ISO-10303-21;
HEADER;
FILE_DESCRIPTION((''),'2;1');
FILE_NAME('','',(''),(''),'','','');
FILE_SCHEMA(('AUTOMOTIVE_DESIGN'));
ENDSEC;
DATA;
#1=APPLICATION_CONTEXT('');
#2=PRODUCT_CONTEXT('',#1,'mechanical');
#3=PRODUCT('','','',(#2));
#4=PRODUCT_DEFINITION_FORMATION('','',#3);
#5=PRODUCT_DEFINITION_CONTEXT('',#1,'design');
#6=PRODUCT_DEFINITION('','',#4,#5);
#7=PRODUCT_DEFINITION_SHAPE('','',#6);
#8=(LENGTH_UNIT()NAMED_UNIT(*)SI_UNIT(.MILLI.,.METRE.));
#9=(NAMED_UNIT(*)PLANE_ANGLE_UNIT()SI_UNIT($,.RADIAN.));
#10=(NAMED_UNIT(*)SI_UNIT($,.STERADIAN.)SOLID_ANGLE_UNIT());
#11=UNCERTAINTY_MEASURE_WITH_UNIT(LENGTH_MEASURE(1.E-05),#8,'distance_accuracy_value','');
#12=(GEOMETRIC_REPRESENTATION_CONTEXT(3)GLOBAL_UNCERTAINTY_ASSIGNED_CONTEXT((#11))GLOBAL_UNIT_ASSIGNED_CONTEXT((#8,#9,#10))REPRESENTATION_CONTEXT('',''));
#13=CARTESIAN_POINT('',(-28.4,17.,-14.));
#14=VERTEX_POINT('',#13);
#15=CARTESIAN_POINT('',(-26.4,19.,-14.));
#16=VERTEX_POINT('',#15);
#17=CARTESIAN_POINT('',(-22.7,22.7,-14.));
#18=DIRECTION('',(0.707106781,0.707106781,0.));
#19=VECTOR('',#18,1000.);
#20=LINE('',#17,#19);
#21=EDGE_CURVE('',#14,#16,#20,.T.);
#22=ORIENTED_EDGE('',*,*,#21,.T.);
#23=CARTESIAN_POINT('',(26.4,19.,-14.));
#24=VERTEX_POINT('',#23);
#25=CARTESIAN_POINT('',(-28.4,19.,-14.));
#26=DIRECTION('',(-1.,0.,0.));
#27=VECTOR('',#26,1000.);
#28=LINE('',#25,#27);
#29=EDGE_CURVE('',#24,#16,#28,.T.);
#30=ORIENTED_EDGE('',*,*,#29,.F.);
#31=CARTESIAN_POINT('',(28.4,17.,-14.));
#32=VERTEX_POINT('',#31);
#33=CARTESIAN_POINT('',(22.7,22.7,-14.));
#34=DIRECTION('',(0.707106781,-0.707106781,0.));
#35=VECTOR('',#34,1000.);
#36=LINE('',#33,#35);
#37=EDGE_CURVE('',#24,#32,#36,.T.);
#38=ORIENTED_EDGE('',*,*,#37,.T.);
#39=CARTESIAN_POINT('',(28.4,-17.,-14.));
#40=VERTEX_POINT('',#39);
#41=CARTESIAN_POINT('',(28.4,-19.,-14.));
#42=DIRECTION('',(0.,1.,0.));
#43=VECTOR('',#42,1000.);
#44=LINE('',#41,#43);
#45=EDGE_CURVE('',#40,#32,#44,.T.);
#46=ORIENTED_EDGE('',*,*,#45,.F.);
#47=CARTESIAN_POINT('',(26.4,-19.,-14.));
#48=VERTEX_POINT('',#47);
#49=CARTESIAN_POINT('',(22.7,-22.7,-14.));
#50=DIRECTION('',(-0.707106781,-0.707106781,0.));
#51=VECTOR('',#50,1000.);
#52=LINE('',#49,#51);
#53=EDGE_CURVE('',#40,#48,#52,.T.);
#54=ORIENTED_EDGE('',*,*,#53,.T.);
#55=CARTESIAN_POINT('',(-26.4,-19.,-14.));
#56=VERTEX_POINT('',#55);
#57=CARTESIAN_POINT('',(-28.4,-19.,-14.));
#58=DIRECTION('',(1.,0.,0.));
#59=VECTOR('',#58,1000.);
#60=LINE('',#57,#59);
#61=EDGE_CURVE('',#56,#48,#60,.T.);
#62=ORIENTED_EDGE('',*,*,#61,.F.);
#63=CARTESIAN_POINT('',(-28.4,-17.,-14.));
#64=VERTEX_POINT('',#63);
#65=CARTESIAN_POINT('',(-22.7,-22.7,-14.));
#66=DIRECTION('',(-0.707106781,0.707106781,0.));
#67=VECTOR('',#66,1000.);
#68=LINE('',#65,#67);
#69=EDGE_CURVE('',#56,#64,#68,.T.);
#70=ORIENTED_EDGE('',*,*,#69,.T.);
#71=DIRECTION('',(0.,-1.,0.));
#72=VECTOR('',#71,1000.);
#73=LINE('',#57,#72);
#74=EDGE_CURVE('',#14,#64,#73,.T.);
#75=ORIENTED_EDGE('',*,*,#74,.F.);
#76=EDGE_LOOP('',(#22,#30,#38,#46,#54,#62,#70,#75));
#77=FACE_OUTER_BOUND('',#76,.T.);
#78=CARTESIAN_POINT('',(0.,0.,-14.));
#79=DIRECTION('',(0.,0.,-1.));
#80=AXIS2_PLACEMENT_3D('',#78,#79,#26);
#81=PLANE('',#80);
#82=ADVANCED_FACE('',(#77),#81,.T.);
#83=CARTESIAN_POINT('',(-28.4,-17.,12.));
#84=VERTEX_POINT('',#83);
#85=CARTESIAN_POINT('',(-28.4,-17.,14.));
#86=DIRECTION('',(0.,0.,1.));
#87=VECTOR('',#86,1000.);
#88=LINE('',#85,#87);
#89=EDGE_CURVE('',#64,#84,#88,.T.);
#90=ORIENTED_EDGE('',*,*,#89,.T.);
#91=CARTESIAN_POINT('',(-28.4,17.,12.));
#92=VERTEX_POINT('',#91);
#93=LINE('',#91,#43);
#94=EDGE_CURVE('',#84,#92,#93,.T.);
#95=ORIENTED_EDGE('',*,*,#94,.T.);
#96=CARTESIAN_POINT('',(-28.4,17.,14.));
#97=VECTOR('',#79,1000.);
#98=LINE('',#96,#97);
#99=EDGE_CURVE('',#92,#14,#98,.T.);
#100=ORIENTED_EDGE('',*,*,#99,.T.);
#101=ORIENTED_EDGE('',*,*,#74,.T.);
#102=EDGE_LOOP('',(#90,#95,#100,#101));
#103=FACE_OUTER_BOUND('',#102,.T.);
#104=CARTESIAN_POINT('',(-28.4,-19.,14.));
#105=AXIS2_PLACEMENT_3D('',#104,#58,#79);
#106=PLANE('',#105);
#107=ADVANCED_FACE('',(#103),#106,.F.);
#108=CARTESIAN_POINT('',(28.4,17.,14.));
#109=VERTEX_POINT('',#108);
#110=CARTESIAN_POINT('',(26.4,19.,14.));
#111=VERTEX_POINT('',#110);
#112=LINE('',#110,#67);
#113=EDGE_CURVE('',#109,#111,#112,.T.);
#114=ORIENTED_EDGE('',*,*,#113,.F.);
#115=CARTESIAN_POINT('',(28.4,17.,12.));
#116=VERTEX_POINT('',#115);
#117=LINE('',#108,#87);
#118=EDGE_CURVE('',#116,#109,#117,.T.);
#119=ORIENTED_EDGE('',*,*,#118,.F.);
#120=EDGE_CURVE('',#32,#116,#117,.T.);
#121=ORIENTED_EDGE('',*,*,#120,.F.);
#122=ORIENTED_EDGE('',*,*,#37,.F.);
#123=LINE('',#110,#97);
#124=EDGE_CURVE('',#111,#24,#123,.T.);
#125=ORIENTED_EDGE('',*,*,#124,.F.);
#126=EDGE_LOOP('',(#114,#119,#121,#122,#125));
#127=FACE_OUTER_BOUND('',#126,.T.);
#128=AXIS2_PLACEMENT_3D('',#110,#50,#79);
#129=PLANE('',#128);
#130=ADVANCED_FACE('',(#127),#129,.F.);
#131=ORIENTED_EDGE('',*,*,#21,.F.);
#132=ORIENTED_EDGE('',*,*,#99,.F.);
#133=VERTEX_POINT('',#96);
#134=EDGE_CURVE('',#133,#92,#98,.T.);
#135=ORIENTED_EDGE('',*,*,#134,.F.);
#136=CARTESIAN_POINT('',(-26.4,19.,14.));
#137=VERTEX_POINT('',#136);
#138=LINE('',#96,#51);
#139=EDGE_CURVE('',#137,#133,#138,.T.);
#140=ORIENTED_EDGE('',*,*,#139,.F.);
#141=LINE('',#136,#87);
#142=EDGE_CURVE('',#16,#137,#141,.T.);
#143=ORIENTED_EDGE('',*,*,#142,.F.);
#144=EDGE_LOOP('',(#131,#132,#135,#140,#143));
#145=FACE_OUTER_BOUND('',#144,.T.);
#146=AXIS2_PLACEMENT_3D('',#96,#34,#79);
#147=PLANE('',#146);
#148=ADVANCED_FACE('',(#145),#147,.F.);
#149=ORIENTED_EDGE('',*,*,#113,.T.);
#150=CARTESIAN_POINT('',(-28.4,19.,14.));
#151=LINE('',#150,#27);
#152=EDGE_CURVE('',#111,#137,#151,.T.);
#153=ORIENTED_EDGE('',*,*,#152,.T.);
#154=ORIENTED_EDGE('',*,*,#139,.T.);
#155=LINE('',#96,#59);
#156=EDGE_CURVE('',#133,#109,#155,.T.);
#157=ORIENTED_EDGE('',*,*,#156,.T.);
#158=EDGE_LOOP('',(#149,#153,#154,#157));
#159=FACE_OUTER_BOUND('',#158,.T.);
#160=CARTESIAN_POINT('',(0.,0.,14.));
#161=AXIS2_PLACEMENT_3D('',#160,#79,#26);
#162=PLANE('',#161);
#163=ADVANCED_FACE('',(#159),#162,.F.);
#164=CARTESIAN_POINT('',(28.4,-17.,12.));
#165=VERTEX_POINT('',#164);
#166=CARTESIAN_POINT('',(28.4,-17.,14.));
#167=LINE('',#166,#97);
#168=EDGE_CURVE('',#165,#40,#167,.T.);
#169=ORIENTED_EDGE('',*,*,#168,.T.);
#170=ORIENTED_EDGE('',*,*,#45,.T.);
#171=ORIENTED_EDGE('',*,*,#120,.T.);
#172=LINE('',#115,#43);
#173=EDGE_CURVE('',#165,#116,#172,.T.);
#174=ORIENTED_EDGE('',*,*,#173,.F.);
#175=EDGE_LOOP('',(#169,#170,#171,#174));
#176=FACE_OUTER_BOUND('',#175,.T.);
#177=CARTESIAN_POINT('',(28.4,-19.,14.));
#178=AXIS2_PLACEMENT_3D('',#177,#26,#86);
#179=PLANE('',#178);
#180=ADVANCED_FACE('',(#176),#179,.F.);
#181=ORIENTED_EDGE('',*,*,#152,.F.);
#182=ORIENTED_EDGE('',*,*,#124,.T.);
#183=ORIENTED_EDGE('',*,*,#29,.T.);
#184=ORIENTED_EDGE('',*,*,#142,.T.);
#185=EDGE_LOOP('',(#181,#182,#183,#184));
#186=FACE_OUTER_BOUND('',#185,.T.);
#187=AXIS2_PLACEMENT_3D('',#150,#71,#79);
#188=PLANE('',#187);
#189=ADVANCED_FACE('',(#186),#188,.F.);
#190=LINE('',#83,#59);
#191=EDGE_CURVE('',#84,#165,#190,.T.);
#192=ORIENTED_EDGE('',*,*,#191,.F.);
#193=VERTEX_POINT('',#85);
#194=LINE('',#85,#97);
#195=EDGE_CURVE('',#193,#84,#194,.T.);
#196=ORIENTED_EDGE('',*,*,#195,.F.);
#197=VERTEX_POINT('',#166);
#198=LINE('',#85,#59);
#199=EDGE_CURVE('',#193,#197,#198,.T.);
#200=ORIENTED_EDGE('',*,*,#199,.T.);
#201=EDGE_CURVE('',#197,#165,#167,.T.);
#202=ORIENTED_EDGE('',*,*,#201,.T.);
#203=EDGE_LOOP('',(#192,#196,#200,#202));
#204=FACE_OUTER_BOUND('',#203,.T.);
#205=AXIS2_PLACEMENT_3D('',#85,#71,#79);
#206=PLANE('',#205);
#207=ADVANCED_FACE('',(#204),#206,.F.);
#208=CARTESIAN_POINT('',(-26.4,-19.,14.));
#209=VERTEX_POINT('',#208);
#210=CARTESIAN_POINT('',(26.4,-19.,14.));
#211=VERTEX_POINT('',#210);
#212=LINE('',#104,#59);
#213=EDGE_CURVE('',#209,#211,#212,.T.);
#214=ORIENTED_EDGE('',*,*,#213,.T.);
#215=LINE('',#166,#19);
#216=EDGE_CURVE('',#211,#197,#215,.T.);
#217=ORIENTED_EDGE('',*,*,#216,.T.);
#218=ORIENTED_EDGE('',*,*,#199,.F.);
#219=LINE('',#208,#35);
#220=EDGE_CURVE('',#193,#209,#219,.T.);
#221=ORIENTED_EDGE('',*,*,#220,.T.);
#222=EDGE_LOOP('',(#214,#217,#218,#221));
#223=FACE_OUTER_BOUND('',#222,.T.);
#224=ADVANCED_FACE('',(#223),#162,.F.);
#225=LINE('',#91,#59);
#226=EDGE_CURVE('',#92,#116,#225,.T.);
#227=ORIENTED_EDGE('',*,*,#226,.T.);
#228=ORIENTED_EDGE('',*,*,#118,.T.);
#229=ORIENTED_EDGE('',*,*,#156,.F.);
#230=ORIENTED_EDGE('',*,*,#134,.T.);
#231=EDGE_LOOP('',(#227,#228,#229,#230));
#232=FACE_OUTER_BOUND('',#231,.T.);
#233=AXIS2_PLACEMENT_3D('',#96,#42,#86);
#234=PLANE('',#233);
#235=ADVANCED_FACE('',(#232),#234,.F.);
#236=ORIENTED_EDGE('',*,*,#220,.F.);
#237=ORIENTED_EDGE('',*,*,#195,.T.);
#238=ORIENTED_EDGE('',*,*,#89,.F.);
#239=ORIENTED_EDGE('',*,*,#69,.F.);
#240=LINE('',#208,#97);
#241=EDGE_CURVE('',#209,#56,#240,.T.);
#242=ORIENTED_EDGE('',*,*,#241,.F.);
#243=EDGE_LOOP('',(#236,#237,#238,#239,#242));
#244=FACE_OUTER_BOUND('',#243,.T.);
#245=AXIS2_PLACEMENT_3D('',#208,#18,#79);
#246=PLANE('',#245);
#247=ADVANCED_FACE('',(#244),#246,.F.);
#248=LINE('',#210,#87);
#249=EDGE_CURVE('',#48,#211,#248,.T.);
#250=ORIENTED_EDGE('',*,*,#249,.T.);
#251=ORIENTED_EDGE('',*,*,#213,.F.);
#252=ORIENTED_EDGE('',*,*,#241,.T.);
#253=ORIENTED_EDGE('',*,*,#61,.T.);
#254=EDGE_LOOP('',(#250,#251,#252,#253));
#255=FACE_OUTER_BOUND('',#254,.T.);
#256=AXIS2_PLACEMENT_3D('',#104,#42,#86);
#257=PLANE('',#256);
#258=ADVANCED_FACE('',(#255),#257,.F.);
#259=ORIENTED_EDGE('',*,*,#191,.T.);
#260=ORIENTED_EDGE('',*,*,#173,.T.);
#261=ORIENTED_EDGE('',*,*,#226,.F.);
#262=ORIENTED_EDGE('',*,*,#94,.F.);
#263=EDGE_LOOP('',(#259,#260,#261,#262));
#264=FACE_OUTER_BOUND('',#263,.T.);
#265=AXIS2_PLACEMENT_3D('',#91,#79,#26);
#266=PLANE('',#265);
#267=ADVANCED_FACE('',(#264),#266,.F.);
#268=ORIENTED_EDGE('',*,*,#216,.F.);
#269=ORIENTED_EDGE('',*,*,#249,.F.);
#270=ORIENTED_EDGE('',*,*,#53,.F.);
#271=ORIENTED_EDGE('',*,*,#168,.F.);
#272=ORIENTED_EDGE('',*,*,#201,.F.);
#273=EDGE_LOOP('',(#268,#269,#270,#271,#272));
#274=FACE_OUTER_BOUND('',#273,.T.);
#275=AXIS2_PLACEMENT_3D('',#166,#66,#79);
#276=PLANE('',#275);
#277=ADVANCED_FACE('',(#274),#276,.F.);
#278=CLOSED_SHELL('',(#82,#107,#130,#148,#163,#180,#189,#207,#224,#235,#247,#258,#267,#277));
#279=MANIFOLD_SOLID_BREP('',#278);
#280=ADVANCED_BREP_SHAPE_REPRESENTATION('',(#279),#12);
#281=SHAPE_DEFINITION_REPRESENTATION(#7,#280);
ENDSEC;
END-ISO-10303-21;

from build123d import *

# Parameters (mm, degrees)
SKETCH_1_W          = 56.8
SKETCH_1_H          = 38
EXTRUDE_1_DEPTH     = 14
CHAMFER_1_SIZE      = 2
SKETCH_2_W          = 2
SKETCH_2_H          = 34
CUT_EXTRUDE_1_DEPTH = 62.508048254


with BuildPart() as part:
    # 草图1 → 凸台-拉伸1 (new, symmetric)
    with BuildSketch(Plane.XY):
        Rectangle(SKETCH_1_W, SKETCH_1_H)
    extrude(amount=EXTRUDE_1_DEPTH, both=True)

    # 倒角1
    chamfer_1_edges = [part.edges().sort_by_distance(p)[0] for p in [
        (28.4, -19, 0),
        (-28.4, -19, 0),
        (-28.4, 19, 0),
        (28.4, 19, 0),
    ]]
    chamfer(chamfer_1_edges, length=CHAMFER_1_SIZE)

    # 草图2 → 切除-拉伸1 (cut, through all)
    with BuildSketch(Plane(origin=(28.4, 0, 0), x_dir=(0, 0, -1), z_dir=(1, 0, 0))):
        with Locations((-13, 0)):
            Rectangle(SKETCH_2_W, SKETCH_2_H)
    extrude(amount=-CUT_EXTRUDE_1_DEPTH, mode=Mode.SUBTRACT)


solid = part.part
